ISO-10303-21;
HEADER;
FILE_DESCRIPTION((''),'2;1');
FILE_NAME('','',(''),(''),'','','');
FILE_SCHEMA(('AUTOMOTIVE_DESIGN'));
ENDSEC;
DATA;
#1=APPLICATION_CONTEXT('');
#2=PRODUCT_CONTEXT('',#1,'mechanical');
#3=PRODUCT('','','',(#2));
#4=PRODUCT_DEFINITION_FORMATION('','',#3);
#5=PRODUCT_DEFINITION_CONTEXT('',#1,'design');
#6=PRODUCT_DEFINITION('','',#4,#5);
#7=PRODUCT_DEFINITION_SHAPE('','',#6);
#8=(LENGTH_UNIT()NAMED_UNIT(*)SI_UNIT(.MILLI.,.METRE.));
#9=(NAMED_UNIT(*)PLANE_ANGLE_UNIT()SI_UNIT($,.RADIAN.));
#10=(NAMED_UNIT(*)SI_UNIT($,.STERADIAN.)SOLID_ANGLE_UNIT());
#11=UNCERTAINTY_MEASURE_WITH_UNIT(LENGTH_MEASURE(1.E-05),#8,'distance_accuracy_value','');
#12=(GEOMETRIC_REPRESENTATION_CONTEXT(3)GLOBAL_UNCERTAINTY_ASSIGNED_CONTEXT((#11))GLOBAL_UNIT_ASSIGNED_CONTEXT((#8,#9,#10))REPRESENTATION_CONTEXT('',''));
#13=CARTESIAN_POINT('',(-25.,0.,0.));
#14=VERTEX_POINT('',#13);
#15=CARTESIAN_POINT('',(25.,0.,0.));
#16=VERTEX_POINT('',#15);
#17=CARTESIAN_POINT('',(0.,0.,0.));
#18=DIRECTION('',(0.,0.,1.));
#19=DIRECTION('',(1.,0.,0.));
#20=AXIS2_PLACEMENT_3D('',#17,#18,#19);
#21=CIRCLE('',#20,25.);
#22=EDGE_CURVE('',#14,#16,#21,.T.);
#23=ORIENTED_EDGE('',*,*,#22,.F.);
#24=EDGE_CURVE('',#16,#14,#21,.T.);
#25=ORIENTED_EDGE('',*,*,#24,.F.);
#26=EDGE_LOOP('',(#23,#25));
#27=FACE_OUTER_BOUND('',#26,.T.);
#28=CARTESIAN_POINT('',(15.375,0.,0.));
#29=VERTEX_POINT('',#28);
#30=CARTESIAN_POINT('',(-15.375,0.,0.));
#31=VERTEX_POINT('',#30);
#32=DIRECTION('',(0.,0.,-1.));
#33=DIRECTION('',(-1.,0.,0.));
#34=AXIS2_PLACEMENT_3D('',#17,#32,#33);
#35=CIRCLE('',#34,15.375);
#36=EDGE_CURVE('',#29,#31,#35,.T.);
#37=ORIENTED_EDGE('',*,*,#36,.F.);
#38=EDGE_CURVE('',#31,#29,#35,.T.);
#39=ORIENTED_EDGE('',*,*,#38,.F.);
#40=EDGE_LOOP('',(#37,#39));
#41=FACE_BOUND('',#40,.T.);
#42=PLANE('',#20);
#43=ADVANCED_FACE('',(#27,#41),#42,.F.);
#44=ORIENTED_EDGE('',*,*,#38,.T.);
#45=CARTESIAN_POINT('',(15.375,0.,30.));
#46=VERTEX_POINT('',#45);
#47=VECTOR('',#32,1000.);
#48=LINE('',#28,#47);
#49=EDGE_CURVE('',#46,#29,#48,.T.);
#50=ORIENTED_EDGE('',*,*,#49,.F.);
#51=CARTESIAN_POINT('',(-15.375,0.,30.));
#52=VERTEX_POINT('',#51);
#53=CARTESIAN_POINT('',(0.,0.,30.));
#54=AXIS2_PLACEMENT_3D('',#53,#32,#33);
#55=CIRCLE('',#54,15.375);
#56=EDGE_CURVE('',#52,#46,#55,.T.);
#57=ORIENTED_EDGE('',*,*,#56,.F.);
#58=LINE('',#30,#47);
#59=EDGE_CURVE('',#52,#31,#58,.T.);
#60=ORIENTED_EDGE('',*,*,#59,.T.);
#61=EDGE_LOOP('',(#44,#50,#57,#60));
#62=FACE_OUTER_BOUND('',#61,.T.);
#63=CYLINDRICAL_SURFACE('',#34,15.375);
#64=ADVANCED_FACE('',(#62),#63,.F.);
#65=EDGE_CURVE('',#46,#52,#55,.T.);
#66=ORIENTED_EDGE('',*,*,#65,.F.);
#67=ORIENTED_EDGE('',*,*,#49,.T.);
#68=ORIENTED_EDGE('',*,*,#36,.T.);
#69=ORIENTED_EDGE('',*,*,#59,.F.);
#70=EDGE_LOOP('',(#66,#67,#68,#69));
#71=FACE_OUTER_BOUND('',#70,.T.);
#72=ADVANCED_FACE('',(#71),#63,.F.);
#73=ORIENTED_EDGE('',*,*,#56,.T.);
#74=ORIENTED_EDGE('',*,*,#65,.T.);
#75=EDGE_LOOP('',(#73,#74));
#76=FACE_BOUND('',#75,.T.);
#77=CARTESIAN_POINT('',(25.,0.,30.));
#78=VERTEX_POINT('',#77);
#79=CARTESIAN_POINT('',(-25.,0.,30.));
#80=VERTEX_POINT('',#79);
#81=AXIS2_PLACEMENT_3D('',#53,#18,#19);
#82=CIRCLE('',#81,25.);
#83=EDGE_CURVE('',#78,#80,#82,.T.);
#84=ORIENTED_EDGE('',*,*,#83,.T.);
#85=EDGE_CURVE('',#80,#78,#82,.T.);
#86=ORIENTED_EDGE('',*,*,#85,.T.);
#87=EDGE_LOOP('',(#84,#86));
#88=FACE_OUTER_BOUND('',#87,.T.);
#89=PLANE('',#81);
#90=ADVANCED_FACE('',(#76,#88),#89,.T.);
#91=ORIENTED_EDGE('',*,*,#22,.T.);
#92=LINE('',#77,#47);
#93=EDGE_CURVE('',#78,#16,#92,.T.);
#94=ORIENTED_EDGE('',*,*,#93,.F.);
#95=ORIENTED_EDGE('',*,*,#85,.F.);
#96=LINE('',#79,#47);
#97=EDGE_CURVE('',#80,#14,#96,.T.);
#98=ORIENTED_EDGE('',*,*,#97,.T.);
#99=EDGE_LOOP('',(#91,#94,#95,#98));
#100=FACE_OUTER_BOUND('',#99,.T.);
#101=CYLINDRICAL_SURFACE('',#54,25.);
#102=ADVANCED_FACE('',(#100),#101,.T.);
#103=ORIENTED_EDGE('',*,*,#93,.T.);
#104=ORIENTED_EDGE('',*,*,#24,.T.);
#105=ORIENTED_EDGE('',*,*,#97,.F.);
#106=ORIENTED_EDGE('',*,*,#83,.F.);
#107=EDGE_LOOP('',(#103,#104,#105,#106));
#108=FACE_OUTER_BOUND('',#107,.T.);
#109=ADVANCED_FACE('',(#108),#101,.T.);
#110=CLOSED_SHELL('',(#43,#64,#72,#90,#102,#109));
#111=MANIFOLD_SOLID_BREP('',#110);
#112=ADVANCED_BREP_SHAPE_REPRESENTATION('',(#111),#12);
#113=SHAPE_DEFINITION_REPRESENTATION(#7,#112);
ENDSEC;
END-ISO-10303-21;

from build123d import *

# Parameters (mm, degrees)
SKETCH1_R           = 25
BOSS_EXTRUDE1_DEPTH = 30
G1_THREADED_HOLE1_D = 30.75


with BuildPart() as part:
    # Sketch1 → Boss-Extrude1 (new body)
    with BuildSketch(Plane.XY):
        Circle(SKETCH1_R)
    extrude(amount=BOSS_EXTRUDE1_DEPTH)

    # G1 Threaded hole1 (through all)
    with Locations(Plane(origin=(0, 0, 0), x_dir=(-1, 0, 0), z_dir=(0, 0, -1))):
        with Locations((0, 0)):
            Hole(G1_THREADED_HOLE1_D / 2)


solid = part.part
